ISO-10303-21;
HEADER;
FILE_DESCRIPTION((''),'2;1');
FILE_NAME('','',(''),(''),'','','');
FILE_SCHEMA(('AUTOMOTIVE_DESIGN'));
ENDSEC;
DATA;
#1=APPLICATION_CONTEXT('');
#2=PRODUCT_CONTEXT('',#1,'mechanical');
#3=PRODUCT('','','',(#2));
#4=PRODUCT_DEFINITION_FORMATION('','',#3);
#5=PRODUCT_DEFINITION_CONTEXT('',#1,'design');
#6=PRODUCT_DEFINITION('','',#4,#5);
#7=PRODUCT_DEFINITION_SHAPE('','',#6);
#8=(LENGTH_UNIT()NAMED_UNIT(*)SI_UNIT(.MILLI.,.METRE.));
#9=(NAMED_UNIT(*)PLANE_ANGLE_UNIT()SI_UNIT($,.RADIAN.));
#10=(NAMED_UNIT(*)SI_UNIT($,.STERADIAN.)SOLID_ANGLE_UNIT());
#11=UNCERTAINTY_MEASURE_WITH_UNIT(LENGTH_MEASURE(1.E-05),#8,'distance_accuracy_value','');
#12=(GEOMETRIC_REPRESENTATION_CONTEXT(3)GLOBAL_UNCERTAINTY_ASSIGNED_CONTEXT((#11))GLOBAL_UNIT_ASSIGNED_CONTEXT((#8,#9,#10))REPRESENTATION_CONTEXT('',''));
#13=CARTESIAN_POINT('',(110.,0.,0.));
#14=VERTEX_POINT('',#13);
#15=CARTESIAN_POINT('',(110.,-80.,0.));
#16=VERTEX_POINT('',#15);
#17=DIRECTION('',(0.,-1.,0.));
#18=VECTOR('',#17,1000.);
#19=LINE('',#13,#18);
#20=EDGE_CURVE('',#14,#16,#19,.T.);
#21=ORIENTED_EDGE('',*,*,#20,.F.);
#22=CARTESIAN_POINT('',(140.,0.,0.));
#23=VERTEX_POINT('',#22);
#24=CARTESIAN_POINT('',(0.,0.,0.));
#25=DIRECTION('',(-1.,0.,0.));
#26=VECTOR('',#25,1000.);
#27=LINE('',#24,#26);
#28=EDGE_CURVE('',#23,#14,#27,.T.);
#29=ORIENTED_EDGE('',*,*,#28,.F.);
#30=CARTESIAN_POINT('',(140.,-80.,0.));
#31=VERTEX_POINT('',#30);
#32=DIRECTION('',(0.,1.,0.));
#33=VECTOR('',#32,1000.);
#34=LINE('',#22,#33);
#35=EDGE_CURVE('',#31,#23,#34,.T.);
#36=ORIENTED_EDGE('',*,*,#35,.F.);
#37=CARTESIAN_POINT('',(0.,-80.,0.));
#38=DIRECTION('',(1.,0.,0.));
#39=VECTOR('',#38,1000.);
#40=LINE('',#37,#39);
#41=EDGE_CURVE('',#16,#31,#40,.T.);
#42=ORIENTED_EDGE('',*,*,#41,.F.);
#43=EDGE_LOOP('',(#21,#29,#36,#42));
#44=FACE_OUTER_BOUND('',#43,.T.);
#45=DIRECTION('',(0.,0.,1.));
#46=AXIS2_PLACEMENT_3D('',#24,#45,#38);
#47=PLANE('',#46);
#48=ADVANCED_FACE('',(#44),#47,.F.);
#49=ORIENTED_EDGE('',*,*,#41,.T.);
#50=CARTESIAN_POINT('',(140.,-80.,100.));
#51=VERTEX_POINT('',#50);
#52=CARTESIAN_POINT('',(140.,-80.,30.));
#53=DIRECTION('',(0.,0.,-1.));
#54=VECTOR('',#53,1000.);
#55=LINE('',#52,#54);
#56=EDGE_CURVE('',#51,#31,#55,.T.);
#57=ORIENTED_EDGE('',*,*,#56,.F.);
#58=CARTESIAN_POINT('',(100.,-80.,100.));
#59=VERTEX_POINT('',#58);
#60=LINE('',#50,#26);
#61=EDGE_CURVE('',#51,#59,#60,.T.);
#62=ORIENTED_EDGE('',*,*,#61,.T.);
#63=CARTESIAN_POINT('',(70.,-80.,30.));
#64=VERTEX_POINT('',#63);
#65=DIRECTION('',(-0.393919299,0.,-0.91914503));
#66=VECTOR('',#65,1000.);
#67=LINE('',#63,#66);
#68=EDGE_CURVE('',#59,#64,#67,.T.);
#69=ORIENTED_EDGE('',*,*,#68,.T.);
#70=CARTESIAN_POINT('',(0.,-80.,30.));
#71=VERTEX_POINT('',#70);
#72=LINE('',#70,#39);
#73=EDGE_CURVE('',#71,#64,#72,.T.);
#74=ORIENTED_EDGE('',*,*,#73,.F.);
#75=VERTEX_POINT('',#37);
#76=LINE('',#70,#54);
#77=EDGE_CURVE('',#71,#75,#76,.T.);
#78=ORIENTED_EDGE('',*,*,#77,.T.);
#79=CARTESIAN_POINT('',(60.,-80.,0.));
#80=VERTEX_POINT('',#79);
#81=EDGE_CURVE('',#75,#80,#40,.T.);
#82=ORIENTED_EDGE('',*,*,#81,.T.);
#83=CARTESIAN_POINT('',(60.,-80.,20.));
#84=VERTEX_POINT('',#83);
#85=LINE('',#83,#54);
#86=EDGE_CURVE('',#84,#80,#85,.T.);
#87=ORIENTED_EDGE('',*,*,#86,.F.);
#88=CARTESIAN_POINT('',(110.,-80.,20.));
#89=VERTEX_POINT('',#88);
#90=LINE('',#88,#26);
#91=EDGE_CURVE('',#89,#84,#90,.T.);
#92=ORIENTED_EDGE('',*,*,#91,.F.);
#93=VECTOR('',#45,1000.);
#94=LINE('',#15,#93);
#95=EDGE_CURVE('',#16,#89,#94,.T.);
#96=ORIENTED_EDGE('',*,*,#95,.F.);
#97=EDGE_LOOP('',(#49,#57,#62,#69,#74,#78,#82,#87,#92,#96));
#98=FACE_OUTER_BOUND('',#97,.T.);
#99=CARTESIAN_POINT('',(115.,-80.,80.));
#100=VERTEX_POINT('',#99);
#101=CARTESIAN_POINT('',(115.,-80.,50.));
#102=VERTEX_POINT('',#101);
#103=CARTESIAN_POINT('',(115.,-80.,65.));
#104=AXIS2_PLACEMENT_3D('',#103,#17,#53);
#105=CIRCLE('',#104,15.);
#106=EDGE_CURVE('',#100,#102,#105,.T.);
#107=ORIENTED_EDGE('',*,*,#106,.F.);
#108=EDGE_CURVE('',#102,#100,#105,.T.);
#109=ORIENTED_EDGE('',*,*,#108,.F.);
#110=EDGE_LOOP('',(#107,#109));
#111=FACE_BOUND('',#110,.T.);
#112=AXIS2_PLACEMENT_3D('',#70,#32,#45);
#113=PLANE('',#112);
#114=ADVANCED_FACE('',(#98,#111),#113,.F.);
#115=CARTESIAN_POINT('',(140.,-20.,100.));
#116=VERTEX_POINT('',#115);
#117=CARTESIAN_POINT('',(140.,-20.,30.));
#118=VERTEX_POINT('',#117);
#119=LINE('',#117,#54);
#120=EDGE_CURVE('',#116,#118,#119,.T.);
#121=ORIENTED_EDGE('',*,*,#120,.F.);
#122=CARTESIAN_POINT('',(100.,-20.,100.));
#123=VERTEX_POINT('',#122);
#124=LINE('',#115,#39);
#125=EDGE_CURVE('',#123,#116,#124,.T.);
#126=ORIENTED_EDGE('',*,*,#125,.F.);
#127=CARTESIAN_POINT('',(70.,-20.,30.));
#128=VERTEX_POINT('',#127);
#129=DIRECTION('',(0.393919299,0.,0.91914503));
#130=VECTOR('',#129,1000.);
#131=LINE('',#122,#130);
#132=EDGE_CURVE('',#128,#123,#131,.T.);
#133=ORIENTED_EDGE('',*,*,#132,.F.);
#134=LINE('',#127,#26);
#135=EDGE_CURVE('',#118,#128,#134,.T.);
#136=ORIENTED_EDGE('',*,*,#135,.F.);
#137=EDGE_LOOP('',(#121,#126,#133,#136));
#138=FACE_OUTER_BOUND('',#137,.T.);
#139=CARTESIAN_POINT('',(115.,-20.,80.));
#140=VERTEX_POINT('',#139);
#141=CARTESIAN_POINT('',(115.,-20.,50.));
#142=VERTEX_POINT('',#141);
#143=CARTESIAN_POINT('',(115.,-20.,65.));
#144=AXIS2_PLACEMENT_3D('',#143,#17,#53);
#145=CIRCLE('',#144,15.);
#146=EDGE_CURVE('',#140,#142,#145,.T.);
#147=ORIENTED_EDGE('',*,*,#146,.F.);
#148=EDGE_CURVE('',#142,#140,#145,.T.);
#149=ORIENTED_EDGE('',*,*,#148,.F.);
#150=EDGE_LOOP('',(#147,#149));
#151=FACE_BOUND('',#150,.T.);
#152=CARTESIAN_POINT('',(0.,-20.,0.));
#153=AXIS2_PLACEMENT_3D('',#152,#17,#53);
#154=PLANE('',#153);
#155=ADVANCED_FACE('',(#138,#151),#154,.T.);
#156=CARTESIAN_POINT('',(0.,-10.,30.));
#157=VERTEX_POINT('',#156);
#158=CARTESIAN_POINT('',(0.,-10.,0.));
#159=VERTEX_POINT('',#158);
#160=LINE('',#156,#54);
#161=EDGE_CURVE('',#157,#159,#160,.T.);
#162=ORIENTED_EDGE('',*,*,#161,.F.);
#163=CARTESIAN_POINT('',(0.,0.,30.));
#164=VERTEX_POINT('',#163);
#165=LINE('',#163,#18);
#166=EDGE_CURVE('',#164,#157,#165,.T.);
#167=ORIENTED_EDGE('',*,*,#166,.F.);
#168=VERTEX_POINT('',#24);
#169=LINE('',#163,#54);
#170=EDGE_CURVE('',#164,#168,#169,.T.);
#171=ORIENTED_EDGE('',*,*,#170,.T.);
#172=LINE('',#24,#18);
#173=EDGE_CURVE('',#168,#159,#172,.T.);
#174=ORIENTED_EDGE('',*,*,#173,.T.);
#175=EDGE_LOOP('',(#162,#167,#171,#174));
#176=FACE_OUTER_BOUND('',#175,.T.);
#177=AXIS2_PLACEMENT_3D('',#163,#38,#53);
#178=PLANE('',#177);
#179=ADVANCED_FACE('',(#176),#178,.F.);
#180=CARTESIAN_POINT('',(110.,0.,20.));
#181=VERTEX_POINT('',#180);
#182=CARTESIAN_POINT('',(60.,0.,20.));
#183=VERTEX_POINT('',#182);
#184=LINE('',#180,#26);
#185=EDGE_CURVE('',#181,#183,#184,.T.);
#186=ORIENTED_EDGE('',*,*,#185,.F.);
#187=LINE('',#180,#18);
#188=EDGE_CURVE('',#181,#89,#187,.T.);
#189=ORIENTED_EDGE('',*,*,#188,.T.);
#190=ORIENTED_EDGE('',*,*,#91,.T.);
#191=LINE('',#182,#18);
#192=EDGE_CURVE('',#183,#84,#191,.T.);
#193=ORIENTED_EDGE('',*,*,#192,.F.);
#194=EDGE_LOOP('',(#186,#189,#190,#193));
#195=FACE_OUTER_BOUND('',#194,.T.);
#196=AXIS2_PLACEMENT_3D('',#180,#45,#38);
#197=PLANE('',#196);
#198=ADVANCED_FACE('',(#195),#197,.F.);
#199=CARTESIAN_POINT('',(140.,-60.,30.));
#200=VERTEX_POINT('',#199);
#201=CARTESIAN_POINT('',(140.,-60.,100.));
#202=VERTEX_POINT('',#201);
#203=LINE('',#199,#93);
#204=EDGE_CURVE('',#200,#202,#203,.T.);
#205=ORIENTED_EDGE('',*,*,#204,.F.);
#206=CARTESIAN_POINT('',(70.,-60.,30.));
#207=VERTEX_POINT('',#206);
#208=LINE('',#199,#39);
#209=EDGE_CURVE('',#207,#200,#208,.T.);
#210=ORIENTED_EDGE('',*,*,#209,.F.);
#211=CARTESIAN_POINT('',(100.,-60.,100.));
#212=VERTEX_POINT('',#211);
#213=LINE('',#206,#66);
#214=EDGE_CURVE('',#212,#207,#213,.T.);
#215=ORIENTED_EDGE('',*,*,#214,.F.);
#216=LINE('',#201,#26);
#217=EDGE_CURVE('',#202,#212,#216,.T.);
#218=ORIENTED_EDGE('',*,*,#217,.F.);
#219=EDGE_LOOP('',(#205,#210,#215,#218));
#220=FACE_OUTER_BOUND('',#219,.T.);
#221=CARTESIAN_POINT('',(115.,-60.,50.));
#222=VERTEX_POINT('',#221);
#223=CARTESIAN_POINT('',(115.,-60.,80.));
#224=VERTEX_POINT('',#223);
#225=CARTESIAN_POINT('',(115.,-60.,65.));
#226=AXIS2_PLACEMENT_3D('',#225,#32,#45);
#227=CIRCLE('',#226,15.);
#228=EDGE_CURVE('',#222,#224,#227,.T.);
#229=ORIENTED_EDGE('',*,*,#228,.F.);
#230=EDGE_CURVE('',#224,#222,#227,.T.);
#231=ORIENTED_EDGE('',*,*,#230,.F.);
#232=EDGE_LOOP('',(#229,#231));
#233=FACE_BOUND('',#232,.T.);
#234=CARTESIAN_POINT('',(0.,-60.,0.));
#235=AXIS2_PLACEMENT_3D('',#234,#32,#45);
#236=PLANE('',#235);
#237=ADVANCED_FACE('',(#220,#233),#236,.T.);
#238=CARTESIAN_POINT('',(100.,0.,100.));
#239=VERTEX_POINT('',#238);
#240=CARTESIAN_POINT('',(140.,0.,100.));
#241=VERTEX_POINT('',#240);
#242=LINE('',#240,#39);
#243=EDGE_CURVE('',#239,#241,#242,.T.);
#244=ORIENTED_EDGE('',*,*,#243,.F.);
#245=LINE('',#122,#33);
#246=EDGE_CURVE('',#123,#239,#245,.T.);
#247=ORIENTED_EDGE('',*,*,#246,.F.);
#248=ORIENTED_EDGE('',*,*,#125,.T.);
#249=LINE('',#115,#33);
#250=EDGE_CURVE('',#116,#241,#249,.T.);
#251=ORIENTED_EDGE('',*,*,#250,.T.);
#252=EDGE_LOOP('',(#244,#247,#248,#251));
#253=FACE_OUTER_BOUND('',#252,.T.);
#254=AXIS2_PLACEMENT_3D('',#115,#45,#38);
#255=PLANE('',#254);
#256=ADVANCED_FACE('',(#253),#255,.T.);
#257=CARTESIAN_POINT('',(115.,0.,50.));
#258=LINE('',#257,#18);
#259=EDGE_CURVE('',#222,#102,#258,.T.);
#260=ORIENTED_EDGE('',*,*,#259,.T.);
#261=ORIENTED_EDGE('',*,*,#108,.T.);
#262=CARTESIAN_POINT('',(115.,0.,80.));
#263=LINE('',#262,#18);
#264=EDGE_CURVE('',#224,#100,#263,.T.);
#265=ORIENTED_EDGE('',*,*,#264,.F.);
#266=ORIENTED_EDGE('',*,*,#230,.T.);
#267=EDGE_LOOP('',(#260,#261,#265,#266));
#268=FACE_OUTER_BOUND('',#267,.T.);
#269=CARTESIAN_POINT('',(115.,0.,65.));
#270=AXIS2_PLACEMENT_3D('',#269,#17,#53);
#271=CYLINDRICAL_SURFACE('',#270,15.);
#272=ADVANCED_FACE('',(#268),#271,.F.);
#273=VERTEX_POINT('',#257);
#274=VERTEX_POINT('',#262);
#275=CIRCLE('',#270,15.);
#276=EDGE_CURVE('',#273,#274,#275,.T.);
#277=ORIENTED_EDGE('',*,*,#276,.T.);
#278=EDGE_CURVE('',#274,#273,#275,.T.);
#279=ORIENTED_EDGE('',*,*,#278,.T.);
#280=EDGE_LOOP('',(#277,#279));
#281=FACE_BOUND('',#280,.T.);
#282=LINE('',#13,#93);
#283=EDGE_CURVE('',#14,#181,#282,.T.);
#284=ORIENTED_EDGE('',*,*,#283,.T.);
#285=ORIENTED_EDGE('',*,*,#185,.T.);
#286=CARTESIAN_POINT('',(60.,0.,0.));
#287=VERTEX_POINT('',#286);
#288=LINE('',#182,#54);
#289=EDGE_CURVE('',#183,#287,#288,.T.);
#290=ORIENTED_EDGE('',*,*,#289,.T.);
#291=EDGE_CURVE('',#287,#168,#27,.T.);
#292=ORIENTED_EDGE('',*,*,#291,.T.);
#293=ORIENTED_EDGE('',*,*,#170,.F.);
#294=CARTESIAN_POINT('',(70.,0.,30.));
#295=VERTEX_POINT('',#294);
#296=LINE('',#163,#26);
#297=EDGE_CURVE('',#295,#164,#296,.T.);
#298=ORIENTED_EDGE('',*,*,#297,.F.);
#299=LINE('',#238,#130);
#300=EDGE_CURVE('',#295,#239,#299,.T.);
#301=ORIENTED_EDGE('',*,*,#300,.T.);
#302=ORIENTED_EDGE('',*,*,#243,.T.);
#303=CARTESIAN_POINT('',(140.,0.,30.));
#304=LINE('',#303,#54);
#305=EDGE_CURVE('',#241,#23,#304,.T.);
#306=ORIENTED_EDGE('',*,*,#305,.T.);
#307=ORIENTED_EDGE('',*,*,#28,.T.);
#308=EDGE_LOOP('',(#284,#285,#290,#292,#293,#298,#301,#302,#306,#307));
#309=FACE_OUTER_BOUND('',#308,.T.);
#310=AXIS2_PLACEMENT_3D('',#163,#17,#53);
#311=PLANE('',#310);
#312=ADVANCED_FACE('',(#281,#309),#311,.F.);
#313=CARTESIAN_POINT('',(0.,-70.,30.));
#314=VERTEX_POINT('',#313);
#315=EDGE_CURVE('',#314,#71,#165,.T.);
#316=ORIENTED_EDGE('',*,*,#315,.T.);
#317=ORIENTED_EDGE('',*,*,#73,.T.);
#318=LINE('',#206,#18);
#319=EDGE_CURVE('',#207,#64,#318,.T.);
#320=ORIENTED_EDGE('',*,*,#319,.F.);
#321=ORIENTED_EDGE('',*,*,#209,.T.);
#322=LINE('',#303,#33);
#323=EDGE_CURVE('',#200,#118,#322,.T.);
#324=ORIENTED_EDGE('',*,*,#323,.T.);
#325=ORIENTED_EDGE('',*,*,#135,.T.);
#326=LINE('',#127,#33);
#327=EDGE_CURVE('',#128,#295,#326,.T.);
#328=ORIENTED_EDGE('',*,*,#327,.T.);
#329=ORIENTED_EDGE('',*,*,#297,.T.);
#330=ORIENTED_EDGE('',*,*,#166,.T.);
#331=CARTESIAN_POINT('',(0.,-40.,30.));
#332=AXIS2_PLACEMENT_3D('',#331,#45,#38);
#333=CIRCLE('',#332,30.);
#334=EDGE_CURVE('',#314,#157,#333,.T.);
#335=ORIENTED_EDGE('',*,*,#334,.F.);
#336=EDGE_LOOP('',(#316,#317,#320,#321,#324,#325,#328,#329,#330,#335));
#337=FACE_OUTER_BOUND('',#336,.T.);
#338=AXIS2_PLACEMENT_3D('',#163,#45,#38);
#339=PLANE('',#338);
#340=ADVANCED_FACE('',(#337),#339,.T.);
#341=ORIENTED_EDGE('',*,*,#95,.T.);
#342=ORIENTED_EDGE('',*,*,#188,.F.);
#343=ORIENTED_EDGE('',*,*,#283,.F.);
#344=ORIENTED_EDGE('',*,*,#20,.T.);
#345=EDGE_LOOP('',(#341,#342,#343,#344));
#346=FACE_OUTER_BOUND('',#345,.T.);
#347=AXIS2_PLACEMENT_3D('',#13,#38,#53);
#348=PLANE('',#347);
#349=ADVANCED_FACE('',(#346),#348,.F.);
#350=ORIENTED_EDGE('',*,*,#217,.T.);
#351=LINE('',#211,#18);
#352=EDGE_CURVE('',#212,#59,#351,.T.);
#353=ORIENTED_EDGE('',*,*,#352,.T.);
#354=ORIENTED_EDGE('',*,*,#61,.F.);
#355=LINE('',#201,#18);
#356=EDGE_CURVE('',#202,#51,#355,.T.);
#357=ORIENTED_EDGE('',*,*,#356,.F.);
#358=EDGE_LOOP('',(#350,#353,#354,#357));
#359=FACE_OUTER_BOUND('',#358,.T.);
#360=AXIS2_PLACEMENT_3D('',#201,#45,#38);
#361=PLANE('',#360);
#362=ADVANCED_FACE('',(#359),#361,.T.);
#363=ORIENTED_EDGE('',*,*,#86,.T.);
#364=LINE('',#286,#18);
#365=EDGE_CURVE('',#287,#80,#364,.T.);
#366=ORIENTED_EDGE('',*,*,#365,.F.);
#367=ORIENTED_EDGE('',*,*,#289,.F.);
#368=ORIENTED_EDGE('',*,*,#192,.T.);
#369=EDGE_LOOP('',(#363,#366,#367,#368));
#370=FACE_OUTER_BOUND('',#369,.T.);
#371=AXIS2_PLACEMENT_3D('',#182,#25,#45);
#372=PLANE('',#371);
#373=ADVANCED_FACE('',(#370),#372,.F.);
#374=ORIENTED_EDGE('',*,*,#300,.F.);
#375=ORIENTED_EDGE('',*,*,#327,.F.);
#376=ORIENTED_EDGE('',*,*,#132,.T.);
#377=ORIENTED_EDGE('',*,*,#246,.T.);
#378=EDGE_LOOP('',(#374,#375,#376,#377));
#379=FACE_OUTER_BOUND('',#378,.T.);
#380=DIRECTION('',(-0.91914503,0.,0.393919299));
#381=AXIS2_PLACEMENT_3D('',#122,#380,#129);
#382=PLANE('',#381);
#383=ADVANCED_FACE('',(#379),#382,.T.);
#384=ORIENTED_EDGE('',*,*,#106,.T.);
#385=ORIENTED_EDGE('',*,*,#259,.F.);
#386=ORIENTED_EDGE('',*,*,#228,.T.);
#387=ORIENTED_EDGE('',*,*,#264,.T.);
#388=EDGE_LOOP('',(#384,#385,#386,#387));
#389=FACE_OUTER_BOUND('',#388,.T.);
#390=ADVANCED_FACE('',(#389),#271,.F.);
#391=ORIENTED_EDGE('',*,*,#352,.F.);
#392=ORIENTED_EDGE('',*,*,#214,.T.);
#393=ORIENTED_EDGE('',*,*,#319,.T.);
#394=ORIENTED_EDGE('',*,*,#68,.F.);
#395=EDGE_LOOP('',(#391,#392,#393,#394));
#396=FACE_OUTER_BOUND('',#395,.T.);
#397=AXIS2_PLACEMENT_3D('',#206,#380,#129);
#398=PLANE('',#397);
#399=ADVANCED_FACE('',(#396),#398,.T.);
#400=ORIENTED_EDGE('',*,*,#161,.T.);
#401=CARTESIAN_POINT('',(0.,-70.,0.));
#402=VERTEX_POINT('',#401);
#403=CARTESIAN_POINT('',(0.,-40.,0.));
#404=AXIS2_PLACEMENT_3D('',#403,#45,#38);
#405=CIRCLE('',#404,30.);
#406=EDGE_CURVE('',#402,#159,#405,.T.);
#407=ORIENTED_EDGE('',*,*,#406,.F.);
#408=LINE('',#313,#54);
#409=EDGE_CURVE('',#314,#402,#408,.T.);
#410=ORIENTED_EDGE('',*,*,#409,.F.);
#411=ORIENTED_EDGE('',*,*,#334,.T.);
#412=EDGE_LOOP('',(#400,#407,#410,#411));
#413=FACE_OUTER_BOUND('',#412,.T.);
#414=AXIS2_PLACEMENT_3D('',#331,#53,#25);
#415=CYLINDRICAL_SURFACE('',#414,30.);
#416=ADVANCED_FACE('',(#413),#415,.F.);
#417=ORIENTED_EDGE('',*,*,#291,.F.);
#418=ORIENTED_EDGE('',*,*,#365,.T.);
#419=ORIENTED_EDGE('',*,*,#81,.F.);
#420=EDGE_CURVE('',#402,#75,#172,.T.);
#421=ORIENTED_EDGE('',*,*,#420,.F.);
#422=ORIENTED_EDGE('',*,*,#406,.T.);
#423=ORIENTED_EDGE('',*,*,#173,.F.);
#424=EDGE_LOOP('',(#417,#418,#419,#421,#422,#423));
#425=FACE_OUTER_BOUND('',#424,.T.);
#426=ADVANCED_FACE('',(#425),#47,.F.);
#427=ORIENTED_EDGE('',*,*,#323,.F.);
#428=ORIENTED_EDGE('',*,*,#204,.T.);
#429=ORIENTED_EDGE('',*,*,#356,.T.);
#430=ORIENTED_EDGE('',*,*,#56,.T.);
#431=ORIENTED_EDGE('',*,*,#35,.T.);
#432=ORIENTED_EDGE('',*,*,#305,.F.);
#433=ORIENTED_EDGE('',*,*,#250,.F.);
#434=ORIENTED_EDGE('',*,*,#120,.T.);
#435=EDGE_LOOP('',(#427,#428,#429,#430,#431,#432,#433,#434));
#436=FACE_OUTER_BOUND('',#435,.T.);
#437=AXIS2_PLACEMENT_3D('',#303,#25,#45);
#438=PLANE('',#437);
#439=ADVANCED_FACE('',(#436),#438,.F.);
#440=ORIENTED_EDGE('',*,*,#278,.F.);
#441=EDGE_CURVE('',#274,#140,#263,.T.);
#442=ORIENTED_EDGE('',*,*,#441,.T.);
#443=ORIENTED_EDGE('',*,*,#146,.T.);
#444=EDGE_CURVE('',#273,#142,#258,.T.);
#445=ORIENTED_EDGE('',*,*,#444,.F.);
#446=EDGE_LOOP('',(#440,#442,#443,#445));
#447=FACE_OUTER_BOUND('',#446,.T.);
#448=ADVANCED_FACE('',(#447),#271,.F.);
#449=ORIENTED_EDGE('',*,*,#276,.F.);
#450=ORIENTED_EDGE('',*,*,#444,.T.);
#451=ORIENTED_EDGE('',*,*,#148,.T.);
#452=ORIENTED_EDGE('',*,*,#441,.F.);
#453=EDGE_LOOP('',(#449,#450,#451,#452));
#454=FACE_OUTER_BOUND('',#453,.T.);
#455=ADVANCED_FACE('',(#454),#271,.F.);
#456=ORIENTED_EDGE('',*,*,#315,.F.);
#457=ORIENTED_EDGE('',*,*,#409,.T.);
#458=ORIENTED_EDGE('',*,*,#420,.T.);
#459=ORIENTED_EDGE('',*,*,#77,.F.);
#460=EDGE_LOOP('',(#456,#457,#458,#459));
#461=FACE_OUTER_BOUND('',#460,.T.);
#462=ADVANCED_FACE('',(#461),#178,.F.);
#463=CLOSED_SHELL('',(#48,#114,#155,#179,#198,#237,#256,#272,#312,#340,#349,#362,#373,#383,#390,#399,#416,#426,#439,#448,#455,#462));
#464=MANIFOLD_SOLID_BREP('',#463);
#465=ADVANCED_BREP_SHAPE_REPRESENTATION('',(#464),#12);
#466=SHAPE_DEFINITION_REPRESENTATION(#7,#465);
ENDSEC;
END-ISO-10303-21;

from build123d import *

# Parameters (mm, degrees)
BASE_BLOCK_DEPTH           = 30
SIDE_BOSS_DEPTH            = 20
TOP_BOSS_DEPTH             = 20
THROUGH_HOLE_SKETCH_R      = 15
COAXIAL_THROUGH_HOLE_DEPTH = 80
CURVED_RELIEF_SKETCH_W     = 50
CURVED_RELIEF_SKETCH_H     = 20
CURVED_RELIEF_CUT_DEPTH    = 80


with BuildPart() as part:
    # Base Profile Sketch → Base Block (new body)
    with BuildSketch(Plane.XY):
        with BuildLine():
            Line((140, 0), (0, 0))
            Line((0, 0), (0, -10))
            ThreePointArc((0, -10), (30, -40), (0, -70))
            Line((0, -70), (0, -80))
            Line((0, -80), (140, -80))
            Line((140, -80), (140, 0))
        make_face()
    extrude(amount=BASE_BLOCK_DEPTH)

    # Side Boss Sketch → Side Boss (add)
    with BuildSketch(Plane.XZ.offset(80)):
        Polygon((140, 30), (140, 100), (100, 100), (70, 30), align=None)
    extrude(amount=-SIDE_BOSS_DEPTH)

    # Top Boss Sketch → Top Boss (add)
    with BuildSketch(Plane(origin=(0, 0, 0), x_dir=(1, 0, 0), z_dir=(0, 1, 0))):
        Polygon((140, -30), (140, -100), (100, -100), (70, -30), align=None)
    extrude(amount=-TOP_BOSS_DEPTH)

    # Through Hole Sketch → Coaxial Through Hole (cut)
    with BuildSketch(Plane.XZ.offset(80)):
        with Locations(Location((115, 65, 0), (0, 0, 270))):
            Circle(THROUGH_HOLE_SKETCH_R)
    extrude(amount=-COAXIAL_THROUGH_HOLE_DEPTH, mode=Mode.SUBTRACT)

    # Curved Relief Sketch → Curved Relief Cut (cut)
    with BuildSketch(Plane.XZ.offset(80)):
        with Locations((85, 10)):
            Rectangle(CURVED_RELIEF_SKETCH_W, CURVED_RELIEF_SKETCH_H)
    extrude(amount=-CURVED_RELIEF_CUT_DEPTH, mode=Mode.SUBTRACT)


solid = part.part
